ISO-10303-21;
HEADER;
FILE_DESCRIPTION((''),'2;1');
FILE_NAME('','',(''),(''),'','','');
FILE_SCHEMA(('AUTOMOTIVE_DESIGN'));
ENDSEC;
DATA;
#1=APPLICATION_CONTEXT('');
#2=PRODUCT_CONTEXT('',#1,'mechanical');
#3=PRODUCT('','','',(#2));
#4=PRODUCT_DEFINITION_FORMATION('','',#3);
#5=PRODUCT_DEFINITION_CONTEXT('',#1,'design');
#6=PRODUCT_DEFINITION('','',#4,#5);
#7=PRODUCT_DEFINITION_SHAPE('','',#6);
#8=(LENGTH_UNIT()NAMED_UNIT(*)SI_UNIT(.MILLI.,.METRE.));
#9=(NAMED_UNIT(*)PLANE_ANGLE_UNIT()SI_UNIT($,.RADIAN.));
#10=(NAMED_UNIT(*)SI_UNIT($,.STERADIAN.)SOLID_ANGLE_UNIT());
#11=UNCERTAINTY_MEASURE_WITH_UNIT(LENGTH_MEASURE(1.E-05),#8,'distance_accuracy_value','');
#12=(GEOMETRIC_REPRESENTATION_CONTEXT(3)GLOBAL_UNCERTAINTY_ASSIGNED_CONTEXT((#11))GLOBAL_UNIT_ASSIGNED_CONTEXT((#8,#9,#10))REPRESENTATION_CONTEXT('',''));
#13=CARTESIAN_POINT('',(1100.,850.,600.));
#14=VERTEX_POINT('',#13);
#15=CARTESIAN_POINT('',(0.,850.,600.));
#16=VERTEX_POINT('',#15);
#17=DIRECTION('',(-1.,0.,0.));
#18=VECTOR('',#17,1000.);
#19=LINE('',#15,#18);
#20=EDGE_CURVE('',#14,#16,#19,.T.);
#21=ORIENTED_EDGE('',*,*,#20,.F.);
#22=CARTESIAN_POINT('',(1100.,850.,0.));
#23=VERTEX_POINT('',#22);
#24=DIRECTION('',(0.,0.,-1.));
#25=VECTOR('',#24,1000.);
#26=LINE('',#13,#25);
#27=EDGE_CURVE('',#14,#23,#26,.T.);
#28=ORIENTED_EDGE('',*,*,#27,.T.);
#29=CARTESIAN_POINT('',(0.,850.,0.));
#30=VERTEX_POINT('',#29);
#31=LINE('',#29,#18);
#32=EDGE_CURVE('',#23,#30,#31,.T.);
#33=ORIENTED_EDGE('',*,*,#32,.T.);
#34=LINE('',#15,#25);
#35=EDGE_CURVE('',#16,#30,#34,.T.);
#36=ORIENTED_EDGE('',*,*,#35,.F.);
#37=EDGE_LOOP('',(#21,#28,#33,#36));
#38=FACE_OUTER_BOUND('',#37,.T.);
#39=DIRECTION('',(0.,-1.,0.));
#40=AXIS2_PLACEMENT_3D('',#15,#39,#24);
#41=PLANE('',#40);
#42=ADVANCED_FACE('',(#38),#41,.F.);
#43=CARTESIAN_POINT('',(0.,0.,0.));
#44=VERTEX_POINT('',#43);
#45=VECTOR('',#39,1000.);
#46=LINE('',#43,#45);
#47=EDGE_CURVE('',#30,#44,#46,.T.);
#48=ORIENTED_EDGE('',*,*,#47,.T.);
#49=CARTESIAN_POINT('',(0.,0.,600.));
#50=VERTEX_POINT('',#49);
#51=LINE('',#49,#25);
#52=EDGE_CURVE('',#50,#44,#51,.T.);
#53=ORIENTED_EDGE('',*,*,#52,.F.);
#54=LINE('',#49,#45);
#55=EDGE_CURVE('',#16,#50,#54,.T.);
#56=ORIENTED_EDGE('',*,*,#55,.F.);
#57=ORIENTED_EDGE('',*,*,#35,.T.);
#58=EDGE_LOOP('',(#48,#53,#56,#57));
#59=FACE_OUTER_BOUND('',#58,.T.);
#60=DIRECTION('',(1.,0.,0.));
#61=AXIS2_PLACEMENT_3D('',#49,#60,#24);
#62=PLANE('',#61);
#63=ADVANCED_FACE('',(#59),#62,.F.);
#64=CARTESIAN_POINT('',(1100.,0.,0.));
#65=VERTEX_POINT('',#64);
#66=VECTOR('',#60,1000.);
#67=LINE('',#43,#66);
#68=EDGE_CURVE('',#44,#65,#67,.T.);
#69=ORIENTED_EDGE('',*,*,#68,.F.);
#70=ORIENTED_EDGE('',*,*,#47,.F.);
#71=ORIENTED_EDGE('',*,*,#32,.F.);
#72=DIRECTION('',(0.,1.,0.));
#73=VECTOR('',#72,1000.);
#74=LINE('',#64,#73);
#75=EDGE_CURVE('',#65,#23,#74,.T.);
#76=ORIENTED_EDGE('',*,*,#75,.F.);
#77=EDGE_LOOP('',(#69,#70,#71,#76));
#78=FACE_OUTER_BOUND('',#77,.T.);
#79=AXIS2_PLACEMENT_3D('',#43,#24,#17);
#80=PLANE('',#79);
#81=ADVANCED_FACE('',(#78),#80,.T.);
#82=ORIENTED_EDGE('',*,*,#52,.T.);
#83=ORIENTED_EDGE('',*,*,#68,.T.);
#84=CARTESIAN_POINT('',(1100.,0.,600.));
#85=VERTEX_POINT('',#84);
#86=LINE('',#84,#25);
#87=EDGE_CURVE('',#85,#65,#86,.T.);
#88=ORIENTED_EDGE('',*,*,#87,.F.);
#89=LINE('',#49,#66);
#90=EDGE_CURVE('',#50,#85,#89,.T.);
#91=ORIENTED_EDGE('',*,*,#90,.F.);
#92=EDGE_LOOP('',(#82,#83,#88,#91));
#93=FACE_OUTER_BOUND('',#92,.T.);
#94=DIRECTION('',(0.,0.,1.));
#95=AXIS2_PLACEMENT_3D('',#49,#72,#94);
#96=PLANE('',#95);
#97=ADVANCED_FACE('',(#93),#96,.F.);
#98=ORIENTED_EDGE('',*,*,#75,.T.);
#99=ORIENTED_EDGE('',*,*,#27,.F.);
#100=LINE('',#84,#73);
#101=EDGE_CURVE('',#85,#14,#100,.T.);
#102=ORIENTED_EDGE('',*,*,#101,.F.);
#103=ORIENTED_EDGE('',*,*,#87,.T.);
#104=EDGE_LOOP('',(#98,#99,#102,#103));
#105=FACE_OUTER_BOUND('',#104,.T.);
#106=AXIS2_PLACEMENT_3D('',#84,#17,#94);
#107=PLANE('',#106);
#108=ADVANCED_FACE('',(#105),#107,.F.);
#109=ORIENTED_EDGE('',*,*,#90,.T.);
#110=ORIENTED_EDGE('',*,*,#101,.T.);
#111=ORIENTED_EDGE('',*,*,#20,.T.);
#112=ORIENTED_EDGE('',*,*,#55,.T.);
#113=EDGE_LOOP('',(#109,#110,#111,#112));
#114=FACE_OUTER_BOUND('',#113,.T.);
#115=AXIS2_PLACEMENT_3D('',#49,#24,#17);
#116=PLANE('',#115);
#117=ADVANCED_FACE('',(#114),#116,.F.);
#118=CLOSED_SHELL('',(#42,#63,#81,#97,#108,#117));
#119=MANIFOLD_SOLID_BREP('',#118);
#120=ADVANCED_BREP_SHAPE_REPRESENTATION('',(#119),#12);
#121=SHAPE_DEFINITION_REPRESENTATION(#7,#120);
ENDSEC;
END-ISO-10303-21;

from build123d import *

# Parameters (mm, degrees)
SKETCH1_W           = 1100
SKETCH1_H           = 850
BOSS_EXTRUDE1_DEPTH = 600


with BuildPart() as part:
    # Sketch1 → Boss-Extrude1 (new body)
    with BuildSketch(Plane.XY):
        with Locations((550, 425)):
            Rectangle(SKETCH1_W, SKETCH1_H)
    extrude(amount=BOSS_EXTRUDE1_DEPTH)


solid = part.part
